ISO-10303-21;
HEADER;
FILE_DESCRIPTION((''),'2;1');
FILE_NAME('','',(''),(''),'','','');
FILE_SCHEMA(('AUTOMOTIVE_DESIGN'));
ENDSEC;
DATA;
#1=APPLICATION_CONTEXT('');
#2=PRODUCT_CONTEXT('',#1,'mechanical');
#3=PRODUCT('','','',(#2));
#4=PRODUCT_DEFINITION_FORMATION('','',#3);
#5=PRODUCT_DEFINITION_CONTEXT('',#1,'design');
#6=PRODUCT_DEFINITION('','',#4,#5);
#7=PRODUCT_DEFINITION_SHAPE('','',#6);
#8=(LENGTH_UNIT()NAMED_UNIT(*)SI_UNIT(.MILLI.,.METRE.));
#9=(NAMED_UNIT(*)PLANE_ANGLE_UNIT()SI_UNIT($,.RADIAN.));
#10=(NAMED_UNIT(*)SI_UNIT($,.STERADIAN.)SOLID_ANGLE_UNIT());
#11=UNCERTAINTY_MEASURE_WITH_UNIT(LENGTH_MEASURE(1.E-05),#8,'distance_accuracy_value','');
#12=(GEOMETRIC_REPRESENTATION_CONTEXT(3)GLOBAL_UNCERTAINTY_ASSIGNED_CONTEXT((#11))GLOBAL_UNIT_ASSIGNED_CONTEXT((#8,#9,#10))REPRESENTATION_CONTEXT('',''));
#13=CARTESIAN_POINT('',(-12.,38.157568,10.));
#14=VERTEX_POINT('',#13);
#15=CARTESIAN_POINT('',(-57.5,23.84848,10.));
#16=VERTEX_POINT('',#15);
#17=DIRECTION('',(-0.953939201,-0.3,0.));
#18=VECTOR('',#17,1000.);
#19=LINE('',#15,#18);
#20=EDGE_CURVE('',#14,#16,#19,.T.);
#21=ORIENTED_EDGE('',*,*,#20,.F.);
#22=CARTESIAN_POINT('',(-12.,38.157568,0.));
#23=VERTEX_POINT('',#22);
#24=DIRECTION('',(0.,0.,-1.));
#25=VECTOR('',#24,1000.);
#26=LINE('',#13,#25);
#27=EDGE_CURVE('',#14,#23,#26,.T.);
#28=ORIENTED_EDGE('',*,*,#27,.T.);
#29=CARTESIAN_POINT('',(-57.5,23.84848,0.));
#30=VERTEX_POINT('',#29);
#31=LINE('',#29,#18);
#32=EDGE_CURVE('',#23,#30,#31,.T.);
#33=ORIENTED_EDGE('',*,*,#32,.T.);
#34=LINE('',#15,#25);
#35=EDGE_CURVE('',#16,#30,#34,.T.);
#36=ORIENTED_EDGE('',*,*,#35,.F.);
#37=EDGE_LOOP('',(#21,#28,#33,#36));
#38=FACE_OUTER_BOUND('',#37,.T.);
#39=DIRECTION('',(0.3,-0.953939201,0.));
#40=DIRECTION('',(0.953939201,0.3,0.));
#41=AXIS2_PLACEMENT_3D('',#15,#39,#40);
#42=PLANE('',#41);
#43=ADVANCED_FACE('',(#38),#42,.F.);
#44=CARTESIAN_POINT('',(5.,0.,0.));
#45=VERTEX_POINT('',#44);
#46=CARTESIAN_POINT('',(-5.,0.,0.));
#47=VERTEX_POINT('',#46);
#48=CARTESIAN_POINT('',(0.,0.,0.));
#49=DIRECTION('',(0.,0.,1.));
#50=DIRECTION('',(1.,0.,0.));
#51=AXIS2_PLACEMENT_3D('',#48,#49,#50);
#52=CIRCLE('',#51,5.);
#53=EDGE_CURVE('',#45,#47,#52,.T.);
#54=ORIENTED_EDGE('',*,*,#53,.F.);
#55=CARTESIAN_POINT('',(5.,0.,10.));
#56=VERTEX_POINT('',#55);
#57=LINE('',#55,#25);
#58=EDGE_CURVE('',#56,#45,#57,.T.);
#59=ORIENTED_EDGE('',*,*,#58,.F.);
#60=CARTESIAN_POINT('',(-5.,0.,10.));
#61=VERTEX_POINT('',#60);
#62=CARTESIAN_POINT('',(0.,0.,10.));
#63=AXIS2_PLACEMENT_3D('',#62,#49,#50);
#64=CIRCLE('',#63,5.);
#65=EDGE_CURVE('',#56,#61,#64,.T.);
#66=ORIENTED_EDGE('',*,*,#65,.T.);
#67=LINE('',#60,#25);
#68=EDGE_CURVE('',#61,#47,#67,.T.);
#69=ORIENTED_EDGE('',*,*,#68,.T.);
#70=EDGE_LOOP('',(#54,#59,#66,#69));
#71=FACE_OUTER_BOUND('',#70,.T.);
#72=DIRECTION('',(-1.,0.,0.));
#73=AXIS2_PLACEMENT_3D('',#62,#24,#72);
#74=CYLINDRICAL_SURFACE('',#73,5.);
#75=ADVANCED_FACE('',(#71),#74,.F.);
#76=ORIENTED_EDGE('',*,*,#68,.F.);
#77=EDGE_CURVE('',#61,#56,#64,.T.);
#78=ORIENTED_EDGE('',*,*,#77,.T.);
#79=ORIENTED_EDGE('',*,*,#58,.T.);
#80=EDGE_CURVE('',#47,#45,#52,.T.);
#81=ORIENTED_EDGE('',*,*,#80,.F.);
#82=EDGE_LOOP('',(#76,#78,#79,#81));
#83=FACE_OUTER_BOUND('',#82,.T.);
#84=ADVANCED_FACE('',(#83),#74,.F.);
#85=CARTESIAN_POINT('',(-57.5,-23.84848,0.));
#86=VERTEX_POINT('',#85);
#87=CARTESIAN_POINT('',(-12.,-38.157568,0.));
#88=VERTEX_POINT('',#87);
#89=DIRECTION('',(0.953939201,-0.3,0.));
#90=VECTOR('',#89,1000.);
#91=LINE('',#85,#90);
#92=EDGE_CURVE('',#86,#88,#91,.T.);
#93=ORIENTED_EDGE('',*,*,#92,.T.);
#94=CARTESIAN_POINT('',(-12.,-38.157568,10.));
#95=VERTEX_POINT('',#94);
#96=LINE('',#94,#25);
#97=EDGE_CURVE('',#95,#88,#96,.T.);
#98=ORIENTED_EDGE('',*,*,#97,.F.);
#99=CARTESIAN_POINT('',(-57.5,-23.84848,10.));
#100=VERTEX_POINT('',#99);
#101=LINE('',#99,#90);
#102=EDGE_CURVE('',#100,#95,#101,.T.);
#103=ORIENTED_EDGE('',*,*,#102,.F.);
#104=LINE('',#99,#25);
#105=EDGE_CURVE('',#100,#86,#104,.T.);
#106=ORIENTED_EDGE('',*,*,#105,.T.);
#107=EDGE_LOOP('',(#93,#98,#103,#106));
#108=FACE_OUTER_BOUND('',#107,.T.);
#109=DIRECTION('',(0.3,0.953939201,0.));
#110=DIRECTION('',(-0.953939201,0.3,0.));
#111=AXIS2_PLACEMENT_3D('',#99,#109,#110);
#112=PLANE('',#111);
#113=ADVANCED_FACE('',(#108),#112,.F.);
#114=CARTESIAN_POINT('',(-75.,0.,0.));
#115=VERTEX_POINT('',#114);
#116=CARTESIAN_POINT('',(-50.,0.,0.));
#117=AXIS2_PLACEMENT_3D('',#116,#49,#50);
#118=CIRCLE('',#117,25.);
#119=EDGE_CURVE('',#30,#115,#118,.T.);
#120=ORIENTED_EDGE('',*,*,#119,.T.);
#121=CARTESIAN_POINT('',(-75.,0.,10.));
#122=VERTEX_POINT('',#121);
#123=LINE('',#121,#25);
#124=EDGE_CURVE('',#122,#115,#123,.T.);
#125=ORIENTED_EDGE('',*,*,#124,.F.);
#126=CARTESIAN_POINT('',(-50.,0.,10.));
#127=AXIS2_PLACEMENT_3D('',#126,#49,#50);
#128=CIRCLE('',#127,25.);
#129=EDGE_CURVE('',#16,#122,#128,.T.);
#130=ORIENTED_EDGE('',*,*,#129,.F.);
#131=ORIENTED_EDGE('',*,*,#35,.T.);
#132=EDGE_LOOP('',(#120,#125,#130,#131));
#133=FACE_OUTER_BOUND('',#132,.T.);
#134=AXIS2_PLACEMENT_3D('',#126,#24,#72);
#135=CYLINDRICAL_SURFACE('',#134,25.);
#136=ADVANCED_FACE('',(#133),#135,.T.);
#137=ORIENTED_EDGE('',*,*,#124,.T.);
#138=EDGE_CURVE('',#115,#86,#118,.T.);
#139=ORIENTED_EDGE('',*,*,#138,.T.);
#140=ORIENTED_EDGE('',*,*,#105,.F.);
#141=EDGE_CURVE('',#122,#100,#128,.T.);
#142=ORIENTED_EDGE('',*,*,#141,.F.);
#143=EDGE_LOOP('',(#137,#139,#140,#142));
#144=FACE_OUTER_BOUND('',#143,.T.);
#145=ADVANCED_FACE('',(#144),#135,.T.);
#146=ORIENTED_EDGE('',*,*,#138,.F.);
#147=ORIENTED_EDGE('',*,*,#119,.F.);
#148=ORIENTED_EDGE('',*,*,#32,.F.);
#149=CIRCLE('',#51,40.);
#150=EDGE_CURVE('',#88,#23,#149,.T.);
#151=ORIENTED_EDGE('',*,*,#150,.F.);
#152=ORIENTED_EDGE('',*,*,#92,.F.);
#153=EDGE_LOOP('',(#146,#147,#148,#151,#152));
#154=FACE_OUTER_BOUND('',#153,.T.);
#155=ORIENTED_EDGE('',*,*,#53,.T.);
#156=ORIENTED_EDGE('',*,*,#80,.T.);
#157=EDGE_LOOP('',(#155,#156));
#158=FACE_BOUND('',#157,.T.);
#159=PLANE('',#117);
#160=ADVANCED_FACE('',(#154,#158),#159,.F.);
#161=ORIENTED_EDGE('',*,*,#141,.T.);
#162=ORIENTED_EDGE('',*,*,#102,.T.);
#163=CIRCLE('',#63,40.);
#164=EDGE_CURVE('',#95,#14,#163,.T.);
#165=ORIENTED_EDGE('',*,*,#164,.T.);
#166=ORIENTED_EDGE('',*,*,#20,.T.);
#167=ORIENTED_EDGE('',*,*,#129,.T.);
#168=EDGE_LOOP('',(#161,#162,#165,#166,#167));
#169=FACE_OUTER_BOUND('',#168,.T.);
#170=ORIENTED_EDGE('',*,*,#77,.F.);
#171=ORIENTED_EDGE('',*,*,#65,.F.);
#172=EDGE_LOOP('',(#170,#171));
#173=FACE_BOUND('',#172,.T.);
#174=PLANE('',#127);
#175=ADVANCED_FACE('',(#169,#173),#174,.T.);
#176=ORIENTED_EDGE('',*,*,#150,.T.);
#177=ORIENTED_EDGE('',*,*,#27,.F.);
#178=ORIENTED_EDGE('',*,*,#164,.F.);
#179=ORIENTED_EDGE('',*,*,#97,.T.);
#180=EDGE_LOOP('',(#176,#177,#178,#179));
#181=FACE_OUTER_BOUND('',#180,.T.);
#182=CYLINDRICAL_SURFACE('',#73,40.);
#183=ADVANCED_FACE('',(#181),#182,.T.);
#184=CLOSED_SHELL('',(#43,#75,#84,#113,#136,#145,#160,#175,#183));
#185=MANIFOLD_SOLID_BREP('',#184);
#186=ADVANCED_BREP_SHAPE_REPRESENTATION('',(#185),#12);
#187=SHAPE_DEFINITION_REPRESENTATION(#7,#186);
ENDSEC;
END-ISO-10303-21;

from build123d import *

# Parameters (mm, degrees)
SKETCH1_R           = 5
BOSS_EXTRUDE1_DEPTH = 10


with BuildPart() as part:
    # Sketch1 → Boss-Extrude1 (new body)
    with BuildSketch(Plane.XY):
        with BuildLine():
            Line((-57.5, 23.848480035), (-12, 38.157568057))
            ThreePointArc((-12, 38.157568057), (40, 0), (-12, -38.157568057))
            Line((-12, -38.157568057), (-57.5, -23.848480035))
            ThreePointArc((-57.5, -23.848480035), (-75, 0), (-57.5, 23.848480035))
        make_face()
        Circle(SKETCH1_R, mode=Mode.SUBTRACT)
    extrude(amount=BOSS_EXTRUDE1_DEPTH)


solid = part.part
